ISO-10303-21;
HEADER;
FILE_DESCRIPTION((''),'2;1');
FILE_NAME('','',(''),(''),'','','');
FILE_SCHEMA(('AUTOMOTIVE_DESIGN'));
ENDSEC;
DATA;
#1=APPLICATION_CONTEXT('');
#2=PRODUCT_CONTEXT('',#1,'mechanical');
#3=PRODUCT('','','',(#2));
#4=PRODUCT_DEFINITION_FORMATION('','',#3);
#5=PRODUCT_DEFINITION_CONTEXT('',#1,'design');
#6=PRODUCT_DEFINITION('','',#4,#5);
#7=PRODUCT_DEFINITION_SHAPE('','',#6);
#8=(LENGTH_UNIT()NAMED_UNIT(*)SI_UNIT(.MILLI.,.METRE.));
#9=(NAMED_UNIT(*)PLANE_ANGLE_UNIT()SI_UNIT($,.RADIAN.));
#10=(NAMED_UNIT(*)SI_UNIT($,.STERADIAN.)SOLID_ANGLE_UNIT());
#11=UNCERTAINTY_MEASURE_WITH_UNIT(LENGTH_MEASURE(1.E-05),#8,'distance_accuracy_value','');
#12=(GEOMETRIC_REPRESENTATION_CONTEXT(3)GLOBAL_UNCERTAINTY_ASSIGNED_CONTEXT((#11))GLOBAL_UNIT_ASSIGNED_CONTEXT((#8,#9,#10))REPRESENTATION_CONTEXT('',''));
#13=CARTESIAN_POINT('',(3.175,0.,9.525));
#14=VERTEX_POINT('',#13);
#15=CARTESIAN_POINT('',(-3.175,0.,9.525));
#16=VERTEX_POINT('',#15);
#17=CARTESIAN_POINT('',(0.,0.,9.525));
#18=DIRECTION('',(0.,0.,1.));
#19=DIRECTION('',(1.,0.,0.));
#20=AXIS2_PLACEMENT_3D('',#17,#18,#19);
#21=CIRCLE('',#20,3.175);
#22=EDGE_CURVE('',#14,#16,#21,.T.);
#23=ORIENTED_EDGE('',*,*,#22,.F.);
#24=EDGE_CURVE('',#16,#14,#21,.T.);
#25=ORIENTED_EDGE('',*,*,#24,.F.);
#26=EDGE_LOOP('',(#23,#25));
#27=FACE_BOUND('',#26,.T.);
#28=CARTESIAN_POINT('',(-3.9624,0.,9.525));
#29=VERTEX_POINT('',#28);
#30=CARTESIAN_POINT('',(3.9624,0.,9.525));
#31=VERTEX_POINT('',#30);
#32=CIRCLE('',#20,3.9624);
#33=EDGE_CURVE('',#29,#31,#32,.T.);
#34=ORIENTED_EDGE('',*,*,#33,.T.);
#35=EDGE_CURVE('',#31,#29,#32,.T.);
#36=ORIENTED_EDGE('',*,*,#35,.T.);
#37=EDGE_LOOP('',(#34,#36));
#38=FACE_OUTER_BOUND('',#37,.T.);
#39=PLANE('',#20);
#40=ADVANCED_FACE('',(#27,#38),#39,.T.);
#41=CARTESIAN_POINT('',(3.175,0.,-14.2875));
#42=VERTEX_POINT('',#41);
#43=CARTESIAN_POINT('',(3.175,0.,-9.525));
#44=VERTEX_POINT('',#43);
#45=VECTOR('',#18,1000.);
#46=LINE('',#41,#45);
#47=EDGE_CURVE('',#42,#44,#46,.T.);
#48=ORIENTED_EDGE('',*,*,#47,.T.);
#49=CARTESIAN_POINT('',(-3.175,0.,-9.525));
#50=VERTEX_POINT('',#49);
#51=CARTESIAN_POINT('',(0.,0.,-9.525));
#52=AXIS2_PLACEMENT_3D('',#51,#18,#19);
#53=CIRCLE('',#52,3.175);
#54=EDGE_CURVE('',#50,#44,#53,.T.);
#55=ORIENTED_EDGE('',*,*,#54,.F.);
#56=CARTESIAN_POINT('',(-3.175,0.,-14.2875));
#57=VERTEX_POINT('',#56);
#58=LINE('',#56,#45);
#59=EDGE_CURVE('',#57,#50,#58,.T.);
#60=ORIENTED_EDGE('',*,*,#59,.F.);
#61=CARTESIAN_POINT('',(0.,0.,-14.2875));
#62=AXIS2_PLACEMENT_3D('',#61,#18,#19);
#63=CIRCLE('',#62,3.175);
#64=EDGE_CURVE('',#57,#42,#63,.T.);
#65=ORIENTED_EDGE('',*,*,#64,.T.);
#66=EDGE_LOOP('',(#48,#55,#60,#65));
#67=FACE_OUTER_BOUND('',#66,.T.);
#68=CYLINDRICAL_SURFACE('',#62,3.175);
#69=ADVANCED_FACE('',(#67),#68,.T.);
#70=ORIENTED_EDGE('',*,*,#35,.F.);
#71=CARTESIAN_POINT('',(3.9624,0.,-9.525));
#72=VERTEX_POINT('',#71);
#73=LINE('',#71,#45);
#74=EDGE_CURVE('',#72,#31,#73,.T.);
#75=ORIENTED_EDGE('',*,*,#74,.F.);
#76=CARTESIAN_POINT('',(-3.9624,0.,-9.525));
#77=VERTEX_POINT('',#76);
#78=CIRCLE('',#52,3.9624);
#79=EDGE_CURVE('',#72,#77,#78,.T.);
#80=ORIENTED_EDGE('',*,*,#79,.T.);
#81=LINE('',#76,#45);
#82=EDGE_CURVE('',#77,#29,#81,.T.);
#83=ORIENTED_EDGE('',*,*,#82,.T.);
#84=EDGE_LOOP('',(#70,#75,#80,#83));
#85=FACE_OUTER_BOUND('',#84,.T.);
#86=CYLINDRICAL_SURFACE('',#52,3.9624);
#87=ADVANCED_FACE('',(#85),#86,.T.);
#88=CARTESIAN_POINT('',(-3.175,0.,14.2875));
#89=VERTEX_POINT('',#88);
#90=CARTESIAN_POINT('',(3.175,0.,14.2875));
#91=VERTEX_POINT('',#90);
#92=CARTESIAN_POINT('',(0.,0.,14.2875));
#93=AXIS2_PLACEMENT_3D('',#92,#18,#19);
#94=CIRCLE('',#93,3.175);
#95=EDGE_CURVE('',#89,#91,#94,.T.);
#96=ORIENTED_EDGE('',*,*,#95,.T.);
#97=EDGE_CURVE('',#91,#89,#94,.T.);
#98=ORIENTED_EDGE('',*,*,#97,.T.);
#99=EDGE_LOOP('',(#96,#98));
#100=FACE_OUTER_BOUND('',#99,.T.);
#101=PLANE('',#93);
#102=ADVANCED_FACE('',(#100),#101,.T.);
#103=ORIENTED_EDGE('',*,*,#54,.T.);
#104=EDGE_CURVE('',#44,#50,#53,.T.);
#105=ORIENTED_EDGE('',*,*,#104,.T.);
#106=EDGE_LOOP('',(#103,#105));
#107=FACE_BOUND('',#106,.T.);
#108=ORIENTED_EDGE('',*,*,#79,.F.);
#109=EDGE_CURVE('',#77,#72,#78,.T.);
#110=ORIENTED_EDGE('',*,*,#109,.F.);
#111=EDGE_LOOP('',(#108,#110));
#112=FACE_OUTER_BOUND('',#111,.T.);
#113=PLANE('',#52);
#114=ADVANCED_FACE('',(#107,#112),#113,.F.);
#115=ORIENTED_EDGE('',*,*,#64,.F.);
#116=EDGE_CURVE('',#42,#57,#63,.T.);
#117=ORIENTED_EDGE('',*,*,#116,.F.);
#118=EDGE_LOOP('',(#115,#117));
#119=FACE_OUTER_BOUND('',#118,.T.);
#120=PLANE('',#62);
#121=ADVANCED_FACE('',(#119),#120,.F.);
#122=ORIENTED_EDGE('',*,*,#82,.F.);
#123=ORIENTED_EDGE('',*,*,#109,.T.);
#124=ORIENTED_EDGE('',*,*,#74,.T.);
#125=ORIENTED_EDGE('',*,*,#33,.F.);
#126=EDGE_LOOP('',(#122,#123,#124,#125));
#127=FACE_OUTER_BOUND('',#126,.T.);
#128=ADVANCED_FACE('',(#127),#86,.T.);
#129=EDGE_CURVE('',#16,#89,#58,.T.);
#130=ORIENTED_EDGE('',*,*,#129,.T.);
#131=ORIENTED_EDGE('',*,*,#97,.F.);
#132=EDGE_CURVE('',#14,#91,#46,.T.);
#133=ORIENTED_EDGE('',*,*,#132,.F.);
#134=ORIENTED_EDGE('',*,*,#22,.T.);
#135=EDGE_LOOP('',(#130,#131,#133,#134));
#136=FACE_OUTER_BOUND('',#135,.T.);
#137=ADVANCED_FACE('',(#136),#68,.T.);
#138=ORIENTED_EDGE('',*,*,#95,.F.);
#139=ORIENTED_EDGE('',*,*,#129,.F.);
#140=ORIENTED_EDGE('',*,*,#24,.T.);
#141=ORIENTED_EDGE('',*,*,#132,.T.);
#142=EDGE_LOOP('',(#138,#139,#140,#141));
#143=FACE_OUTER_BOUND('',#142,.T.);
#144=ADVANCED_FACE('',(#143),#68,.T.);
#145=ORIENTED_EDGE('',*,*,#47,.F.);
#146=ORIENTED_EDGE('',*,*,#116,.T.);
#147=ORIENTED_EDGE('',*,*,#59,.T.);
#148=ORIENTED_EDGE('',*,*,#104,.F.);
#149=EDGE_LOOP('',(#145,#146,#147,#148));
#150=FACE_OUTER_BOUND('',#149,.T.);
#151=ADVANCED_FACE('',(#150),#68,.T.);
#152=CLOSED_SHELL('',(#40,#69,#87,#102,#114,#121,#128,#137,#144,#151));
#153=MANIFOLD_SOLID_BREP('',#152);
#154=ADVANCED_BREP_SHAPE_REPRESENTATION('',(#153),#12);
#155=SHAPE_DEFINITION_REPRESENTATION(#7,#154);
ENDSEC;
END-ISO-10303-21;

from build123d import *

# Parameters (mm, degrees)
BOSS_EXTRUDE1_DEPTH      = 9.525
BOSS_EXTRUDE1_DEPTH_BACK = 9.525
SKETCH1_R                = 3.9624
BOSS_EXTRUDE2_DEPTH      = 14.2875
BOSS_EXTRUDE2_DEPTH_BACK = 14.2875
BOSS_EXTRUDE2_START      = -9.525
SKETCH2_R                = 3.175


with BuildPart() as part:
    # Sketch1 → Boss-Extrude1 (new, two sides: drawn at the far end of the back side and taken through both)
    with BuildSketch(Plane.XY.offset(-BOSS_EXTRUDE1_DEPTH_BACK)):
        Circle(SKETCH1_R)
    extrude(amount=BOSS_EXTRUDE1_DEPTH + BOSS_EXTRUDE1_DEPTH_BACK)

    # Sketch2 → Boss-Extrude2 (add, two sides: drawn at the far end of the back side and taken through both)
    with BuildSketch(Plane.XY.offset(9.525).offset(BOSS_EXTRUDE2_START - BOSS_EXTRUDE2_DEPTH_BACK)):
        Circle(SKETCH2_R)
    extrude(amount=BOSS_EXTRUDE2_DEPTH + BOSS_EXTRUDE2_DEPTH_BACK)


solid = part.part
